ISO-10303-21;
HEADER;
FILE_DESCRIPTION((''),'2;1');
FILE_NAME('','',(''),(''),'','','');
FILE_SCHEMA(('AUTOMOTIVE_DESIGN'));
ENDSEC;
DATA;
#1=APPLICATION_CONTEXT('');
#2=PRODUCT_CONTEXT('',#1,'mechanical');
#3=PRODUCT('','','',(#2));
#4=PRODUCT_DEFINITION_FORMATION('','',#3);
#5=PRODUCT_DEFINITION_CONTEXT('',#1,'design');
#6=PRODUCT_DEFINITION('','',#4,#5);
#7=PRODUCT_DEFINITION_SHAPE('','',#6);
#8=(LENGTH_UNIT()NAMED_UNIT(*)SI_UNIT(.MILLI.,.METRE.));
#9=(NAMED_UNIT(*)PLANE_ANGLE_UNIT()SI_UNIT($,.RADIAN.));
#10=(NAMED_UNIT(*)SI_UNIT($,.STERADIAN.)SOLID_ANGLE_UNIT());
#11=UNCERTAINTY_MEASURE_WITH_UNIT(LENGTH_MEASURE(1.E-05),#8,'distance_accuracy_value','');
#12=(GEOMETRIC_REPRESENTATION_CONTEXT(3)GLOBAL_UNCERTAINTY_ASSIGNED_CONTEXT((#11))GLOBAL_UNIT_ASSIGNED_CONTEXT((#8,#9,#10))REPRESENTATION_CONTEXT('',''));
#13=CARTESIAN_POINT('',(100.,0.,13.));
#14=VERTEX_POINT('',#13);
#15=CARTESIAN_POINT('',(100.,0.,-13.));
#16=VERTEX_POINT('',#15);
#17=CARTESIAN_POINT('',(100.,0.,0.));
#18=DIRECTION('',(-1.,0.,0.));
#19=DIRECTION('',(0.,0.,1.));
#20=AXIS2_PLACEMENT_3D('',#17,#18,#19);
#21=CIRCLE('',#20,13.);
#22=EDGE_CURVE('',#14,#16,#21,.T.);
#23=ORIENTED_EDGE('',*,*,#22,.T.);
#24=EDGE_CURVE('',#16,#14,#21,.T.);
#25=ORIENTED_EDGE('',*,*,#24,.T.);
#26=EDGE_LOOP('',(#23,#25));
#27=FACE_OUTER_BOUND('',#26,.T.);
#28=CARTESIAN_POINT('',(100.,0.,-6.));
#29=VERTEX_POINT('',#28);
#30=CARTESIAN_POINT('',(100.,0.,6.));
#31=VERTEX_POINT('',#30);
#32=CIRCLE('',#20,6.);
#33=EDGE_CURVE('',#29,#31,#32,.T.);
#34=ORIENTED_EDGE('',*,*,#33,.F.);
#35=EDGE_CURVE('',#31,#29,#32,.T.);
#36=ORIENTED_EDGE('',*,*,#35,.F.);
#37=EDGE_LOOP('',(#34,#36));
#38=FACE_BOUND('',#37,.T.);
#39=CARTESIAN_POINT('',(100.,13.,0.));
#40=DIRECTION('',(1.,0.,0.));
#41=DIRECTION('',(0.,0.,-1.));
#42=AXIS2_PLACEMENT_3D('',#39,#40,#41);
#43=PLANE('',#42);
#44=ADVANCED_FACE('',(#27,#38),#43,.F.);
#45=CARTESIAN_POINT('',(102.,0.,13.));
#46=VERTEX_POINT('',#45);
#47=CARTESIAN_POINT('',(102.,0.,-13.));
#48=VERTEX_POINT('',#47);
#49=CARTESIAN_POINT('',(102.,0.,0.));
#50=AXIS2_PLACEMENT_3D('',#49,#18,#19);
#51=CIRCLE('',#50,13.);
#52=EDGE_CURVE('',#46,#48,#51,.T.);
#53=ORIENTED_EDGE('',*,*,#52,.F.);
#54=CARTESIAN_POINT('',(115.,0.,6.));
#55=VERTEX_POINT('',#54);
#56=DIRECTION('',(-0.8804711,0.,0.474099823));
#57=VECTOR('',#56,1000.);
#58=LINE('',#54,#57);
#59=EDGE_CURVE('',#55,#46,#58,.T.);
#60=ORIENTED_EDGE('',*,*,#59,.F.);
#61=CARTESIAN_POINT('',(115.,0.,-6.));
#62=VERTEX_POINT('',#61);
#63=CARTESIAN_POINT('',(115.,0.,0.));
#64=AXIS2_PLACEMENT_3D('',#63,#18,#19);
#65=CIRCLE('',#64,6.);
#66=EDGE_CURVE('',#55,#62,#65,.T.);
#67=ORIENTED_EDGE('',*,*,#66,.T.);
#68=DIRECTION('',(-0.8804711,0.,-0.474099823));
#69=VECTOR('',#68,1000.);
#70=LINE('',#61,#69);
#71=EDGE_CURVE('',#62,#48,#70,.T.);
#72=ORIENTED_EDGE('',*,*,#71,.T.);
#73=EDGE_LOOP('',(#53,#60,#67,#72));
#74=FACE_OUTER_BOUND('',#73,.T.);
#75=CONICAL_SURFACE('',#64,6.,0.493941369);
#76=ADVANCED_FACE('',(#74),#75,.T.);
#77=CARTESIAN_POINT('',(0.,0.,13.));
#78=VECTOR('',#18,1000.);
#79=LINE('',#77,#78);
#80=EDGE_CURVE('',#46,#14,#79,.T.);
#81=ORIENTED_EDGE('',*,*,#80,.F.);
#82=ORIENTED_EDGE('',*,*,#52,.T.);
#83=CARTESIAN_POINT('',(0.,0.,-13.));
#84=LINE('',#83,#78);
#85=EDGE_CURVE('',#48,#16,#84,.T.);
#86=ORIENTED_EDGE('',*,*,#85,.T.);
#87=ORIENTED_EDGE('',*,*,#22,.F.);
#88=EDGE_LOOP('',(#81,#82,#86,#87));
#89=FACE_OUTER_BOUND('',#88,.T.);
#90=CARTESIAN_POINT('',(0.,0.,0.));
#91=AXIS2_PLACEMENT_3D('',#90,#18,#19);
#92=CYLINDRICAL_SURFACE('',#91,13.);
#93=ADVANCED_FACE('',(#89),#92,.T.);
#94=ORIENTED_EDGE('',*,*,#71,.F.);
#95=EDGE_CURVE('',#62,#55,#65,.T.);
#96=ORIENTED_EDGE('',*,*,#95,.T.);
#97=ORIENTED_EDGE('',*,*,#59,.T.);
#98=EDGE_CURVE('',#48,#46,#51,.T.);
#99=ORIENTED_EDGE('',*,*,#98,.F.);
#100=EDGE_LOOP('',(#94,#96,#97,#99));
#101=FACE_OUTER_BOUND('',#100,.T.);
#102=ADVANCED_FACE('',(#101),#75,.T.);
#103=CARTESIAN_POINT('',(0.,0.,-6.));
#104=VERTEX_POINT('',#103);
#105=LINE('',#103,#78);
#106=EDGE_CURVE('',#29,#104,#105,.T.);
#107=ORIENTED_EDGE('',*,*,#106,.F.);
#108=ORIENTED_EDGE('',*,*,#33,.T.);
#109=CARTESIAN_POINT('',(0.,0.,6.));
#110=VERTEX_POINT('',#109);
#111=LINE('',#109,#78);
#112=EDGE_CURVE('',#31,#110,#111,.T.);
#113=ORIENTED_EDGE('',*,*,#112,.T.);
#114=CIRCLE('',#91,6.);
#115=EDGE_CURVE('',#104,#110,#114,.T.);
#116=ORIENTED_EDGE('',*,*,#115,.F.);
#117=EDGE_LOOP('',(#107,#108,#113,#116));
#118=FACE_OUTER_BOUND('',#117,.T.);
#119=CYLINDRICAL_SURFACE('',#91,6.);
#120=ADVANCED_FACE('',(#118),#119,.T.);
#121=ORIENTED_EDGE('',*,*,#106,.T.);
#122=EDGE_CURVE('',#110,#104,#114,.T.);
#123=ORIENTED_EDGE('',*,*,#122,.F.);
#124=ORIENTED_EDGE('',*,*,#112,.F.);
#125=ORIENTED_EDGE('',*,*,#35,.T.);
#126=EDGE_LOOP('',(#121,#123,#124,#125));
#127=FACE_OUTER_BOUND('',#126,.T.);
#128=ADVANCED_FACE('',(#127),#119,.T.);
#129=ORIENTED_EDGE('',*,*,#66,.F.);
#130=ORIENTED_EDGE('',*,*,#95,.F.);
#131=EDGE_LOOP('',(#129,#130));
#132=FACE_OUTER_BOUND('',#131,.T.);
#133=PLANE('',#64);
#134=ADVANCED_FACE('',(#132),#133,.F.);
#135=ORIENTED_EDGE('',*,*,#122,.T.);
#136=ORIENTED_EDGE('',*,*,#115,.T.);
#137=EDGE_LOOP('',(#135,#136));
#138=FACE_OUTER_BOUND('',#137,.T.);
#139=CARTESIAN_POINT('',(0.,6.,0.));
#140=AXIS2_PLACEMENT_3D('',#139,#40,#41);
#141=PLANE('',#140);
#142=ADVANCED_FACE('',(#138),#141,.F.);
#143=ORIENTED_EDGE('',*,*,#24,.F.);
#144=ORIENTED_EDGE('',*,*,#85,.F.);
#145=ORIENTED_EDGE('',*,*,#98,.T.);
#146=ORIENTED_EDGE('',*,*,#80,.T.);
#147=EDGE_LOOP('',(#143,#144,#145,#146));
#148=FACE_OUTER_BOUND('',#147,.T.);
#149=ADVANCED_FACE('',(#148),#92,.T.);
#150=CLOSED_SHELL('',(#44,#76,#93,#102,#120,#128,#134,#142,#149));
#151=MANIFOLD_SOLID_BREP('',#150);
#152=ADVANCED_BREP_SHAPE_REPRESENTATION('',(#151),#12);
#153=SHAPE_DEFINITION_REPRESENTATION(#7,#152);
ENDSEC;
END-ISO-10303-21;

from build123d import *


with BuildPart() as part:
    # Rod Profile Sketch → Rod Body Revolve (revolve)
    with BuildSketch(Plane.XY, mode=Mode.PRIVATE) as rod_body_revolve_sk:
        Polygon((0, 0), (115, 0), (115, 6), (102, 13), (100, 13), (100, 6), (0, 6), align=None)
    revolve(rod_body_revolve_sk.sketch.rotate(Axis((0, 0, 0), (1, 0, 0)), 90), axis=Axis((0, 0, 0), (1, 0, 0)))


solid = part.part
